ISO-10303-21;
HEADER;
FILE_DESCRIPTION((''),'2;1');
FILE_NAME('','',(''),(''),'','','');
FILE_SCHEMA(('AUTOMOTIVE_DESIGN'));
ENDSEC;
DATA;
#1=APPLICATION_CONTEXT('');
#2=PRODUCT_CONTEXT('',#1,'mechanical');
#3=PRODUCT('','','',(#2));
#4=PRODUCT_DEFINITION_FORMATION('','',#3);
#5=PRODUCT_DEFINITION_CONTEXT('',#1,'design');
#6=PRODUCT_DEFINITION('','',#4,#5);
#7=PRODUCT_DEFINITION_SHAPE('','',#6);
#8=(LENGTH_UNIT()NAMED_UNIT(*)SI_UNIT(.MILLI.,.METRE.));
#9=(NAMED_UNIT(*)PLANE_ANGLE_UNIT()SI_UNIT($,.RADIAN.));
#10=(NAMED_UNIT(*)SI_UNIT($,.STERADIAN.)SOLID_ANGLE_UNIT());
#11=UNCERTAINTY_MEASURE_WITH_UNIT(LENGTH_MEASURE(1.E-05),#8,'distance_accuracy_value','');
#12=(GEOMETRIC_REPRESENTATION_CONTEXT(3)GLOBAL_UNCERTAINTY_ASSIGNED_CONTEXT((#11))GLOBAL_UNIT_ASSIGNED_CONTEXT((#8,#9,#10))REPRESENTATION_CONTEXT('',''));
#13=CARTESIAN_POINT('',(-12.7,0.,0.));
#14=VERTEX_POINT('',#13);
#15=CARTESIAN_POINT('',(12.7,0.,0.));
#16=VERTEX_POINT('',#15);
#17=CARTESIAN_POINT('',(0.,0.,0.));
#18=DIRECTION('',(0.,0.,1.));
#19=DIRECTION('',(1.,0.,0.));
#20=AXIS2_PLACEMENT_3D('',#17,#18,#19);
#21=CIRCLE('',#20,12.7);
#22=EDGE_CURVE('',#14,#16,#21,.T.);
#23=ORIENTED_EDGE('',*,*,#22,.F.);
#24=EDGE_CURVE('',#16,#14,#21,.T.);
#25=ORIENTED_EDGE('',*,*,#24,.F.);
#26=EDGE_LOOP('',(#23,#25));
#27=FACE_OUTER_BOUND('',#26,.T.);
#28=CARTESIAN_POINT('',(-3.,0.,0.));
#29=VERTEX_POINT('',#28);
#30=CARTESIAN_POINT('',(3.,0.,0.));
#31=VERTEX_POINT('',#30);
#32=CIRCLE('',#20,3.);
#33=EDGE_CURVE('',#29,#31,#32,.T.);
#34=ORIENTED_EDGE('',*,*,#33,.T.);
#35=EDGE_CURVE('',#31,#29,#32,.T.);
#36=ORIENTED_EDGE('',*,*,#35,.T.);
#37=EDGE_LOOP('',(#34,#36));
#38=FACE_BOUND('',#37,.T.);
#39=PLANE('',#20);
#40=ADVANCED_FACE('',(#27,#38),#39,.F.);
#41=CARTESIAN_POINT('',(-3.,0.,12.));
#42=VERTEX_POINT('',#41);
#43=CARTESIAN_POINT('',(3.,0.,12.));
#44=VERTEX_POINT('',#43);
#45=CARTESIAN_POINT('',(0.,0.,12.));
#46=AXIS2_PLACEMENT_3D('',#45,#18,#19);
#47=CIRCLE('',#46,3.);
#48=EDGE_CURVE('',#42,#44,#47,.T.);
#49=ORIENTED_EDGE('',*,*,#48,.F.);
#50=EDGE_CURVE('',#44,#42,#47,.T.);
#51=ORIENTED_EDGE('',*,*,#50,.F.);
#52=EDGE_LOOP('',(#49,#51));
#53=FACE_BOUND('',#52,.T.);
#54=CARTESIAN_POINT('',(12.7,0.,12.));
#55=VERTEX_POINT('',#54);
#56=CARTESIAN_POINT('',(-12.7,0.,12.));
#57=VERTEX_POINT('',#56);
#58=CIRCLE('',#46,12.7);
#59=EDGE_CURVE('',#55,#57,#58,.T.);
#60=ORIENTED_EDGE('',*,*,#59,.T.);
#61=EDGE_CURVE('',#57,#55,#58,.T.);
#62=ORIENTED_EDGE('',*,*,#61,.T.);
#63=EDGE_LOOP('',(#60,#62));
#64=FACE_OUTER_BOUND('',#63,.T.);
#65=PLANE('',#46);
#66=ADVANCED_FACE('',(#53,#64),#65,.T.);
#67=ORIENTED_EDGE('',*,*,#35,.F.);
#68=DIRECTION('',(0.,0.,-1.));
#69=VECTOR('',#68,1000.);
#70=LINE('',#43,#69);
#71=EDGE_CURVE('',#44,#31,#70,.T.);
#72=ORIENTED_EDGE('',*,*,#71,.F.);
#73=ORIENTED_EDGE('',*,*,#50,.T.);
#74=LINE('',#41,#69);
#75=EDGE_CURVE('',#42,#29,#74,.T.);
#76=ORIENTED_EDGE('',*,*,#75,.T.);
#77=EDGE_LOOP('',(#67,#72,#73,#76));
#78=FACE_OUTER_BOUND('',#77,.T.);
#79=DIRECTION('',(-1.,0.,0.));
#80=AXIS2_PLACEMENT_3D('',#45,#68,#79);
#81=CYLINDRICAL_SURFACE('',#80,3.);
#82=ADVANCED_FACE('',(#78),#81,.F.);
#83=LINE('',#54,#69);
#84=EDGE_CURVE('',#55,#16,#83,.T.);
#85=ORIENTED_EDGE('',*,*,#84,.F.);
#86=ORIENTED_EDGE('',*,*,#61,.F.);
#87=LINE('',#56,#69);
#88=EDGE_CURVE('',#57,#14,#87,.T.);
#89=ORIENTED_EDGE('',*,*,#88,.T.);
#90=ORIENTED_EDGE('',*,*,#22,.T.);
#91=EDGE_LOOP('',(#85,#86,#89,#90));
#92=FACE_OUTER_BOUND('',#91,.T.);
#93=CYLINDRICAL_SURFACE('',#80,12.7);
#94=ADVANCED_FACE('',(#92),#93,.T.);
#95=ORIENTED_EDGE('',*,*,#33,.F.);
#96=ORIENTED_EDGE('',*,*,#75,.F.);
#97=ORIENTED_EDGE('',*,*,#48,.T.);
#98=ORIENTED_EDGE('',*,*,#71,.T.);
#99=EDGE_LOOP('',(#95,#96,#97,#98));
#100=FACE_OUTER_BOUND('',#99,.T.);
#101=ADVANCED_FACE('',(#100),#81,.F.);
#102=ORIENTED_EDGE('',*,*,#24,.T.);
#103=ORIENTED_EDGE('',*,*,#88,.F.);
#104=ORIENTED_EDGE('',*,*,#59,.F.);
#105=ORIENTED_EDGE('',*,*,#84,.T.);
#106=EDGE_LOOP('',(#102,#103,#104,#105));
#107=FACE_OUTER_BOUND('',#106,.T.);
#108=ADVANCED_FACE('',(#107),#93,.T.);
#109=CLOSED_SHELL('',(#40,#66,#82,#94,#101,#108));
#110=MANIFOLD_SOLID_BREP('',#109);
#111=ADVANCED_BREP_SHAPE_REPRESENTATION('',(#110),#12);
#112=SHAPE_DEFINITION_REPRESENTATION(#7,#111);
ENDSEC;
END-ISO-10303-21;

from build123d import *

# Parameters (mm, degrees)
SKETCH1_R           = 12.7
SKETCH1_R_2         = 3
BOSS_EXTRUDE1_DEPTH = 12


with BuildPart() as part:
    # Sketch1 → Boss-Extrude1 (new body)
    with BuildSketch(Plane.XY):
        Circle(SKETCH1_R)
        Circle(SKETCH1_R_2, mode=Mode.SUBTRACT)
    extrude(amount=BOSS_EXTRUDE1_DEPTH)


solid = part.part
